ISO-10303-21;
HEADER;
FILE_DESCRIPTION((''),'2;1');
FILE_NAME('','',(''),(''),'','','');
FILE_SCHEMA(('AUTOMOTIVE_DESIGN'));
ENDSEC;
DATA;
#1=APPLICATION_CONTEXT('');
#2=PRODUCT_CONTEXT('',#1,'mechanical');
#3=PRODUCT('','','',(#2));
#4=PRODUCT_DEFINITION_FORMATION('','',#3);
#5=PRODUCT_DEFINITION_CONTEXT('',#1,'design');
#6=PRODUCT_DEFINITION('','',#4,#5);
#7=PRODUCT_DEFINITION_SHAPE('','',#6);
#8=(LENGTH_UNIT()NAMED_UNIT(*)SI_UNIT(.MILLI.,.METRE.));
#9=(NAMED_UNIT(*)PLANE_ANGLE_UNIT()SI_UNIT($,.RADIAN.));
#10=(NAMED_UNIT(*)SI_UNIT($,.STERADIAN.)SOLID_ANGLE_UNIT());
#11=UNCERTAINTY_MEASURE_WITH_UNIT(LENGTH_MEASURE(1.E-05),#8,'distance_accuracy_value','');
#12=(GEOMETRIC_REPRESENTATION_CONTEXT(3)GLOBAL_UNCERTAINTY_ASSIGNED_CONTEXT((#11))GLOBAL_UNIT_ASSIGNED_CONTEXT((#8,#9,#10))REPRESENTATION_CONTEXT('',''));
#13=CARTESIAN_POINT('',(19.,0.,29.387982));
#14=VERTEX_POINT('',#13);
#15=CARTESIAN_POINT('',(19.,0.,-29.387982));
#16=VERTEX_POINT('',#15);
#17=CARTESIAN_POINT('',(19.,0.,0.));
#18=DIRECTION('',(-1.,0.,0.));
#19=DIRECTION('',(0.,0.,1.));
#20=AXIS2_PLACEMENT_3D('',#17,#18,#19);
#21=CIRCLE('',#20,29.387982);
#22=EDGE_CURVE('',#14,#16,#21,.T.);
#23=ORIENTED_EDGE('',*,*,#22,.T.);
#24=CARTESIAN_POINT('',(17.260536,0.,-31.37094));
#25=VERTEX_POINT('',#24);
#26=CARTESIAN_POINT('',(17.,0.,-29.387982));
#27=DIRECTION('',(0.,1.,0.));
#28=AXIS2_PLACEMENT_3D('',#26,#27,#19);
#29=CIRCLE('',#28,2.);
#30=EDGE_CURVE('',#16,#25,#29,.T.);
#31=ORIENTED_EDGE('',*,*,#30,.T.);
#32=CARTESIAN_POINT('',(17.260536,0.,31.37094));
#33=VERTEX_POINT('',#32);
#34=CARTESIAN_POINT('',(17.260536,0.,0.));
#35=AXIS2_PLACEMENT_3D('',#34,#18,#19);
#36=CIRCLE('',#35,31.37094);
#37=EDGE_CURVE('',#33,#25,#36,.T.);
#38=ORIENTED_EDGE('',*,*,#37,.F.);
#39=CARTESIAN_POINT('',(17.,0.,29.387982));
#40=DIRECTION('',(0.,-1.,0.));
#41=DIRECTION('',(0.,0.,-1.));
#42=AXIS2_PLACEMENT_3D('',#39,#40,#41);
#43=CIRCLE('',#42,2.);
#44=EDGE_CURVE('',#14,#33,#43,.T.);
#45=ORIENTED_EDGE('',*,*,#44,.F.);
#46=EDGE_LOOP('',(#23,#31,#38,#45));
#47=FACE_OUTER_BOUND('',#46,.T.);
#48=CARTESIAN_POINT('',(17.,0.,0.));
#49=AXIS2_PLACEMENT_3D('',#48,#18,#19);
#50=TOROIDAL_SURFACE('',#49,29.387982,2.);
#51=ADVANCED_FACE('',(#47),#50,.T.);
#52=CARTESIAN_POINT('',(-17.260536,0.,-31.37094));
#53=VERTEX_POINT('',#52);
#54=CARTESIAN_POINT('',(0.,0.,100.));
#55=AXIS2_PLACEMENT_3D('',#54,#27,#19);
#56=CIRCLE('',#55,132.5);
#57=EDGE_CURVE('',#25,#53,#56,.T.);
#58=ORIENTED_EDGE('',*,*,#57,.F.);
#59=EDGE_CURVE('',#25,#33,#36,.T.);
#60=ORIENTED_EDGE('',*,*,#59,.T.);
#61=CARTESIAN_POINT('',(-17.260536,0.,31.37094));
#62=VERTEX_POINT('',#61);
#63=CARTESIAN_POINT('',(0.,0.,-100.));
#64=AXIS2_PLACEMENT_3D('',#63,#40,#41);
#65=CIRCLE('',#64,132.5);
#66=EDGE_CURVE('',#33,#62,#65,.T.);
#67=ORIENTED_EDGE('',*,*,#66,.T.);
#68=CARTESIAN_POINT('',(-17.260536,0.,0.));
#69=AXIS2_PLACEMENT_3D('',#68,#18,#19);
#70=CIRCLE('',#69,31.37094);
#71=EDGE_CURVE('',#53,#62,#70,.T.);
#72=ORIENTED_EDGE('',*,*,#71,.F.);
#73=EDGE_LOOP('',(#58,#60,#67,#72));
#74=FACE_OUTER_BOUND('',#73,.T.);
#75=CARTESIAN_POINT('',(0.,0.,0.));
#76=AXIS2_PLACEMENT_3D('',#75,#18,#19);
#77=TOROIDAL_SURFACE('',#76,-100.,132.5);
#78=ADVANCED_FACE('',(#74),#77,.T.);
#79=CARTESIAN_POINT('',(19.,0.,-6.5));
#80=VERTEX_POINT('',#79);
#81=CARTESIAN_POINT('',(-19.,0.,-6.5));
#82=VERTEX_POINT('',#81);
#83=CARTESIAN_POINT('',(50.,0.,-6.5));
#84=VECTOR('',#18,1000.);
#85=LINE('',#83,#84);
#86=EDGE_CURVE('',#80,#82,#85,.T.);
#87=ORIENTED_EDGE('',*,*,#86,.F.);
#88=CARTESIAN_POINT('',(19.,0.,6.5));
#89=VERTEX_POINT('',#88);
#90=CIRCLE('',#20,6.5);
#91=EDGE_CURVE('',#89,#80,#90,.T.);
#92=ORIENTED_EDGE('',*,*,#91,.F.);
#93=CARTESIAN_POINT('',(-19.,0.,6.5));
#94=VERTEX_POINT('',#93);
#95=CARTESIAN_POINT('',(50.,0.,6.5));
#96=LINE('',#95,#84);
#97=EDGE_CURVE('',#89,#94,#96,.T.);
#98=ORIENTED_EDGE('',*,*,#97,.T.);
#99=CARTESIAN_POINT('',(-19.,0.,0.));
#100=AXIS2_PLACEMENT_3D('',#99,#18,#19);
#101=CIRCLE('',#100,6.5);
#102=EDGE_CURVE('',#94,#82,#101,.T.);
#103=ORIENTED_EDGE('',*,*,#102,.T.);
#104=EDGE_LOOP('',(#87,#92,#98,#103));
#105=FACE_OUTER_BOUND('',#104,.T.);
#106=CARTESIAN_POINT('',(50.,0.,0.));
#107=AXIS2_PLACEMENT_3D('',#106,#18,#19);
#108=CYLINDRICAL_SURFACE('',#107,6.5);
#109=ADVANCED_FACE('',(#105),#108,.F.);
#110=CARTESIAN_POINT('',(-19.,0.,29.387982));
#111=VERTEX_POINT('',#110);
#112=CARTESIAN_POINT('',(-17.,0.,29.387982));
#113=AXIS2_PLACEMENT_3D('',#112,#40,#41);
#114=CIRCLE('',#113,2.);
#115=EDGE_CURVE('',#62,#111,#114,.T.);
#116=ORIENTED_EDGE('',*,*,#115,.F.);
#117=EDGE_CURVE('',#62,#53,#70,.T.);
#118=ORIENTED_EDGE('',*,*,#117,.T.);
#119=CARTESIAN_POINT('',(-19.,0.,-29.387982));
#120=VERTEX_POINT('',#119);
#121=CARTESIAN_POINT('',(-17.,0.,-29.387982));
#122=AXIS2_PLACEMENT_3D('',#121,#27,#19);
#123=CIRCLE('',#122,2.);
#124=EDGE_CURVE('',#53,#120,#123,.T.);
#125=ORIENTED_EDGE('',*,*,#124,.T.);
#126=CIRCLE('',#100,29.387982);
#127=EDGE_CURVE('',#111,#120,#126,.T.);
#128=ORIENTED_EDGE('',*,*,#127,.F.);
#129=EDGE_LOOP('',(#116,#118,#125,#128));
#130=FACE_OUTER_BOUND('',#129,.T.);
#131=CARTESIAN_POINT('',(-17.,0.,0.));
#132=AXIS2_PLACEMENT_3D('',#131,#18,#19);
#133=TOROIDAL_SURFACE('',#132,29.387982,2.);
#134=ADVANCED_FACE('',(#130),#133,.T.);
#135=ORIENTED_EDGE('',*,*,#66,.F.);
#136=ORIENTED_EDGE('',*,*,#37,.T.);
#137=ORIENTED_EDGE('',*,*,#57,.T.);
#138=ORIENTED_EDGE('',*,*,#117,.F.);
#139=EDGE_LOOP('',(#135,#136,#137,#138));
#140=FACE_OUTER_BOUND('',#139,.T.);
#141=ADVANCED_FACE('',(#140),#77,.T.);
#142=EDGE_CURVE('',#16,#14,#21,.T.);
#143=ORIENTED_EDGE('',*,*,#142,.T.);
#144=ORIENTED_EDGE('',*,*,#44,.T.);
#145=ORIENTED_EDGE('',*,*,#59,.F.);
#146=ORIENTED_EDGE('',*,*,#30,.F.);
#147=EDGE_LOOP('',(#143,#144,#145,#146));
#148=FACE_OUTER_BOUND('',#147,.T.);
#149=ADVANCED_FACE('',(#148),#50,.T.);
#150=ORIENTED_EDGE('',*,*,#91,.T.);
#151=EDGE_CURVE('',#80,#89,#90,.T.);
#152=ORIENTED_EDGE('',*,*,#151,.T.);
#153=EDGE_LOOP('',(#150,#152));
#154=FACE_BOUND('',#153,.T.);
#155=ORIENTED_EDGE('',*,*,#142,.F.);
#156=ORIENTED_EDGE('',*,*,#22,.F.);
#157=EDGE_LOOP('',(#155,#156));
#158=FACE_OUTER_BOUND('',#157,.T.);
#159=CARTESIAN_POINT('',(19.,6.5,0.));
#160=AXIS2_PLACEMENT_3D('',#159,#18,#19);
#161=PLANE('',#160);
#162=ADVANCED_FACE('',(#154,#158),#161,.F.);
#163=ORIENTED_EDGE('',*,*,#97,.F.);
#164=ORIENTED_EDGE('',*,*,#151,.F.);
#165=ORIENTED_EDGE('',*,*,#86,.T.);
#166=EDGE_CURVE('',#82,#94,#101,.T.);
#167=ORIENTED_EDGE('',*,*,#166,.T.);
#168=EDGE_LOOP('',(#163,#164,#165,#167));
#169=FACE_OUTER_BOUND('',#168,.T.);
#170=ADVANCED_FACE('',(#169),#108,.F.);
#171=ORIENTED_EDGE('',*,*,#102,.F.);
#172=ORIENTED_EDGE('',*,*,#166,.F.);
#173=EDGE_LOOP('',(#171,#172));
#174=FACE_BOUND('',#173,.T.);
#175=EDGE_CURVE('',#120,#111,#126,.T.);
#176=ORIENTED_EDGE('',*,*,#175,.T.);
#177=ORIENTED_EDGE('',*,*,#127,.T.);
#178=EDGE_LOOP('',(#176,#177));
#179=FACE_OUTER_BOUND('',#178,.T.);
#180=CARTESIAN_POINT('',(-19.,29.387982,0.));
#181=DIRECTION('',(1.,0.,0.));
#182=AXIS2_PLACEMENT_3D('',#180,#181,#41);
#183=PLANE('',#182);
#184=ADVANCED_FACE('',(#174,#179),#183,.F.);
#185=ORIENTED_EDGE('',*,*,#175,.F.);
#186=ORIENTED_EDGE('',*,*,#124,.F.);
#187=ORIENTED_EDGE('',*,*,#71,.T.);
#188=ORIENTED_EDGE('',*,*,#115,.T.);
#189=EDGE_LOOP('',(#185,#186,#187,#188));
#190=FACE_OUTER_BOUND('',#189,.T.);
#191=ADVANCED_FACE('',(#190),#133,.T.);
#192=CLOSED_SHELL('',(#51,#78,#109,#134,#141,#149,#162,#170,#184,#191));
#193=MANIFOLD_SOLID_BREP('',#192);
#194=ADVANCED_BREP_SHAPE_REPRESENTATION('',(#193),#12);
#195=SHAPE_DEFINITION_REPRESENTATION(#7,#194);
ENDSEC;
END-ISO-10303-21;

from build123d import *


with BuildPart() as part:
    # 草图1 → 旋转1 (revolve)
    with BuildSketch(Plane.XY, mode=Mode.PRIVATE) as revolve_1_sk:
        with BuildLine():
            Line((-19, 6.5), (19, 6.5))
            Line((19, 6.5), (19, 29.38798244))
            ThreePointArc((19, 29.38798244), (18.503508031, 30.706869699), (17.260536398, 31.370940026))
            ThreePointArc((17.260536398, 31.370940026), (0, 32.5), (-17.260536398, 31.370940026))
            ThreePointArc((-17.260536398, 31.370940026), (-18.503508031, 30.706869699), (-19, 29.38798244))
            Line((-19, 29.38798244), (-19, 6.5))
        make_face()
    revolve(revolve_1_sk.sketch.rotate(Axis((50, 0, 0), (-1, 0, 0)), 270), axis=Axis((50, 0, 0), (-1, 0, 0)))


solid = part.part
